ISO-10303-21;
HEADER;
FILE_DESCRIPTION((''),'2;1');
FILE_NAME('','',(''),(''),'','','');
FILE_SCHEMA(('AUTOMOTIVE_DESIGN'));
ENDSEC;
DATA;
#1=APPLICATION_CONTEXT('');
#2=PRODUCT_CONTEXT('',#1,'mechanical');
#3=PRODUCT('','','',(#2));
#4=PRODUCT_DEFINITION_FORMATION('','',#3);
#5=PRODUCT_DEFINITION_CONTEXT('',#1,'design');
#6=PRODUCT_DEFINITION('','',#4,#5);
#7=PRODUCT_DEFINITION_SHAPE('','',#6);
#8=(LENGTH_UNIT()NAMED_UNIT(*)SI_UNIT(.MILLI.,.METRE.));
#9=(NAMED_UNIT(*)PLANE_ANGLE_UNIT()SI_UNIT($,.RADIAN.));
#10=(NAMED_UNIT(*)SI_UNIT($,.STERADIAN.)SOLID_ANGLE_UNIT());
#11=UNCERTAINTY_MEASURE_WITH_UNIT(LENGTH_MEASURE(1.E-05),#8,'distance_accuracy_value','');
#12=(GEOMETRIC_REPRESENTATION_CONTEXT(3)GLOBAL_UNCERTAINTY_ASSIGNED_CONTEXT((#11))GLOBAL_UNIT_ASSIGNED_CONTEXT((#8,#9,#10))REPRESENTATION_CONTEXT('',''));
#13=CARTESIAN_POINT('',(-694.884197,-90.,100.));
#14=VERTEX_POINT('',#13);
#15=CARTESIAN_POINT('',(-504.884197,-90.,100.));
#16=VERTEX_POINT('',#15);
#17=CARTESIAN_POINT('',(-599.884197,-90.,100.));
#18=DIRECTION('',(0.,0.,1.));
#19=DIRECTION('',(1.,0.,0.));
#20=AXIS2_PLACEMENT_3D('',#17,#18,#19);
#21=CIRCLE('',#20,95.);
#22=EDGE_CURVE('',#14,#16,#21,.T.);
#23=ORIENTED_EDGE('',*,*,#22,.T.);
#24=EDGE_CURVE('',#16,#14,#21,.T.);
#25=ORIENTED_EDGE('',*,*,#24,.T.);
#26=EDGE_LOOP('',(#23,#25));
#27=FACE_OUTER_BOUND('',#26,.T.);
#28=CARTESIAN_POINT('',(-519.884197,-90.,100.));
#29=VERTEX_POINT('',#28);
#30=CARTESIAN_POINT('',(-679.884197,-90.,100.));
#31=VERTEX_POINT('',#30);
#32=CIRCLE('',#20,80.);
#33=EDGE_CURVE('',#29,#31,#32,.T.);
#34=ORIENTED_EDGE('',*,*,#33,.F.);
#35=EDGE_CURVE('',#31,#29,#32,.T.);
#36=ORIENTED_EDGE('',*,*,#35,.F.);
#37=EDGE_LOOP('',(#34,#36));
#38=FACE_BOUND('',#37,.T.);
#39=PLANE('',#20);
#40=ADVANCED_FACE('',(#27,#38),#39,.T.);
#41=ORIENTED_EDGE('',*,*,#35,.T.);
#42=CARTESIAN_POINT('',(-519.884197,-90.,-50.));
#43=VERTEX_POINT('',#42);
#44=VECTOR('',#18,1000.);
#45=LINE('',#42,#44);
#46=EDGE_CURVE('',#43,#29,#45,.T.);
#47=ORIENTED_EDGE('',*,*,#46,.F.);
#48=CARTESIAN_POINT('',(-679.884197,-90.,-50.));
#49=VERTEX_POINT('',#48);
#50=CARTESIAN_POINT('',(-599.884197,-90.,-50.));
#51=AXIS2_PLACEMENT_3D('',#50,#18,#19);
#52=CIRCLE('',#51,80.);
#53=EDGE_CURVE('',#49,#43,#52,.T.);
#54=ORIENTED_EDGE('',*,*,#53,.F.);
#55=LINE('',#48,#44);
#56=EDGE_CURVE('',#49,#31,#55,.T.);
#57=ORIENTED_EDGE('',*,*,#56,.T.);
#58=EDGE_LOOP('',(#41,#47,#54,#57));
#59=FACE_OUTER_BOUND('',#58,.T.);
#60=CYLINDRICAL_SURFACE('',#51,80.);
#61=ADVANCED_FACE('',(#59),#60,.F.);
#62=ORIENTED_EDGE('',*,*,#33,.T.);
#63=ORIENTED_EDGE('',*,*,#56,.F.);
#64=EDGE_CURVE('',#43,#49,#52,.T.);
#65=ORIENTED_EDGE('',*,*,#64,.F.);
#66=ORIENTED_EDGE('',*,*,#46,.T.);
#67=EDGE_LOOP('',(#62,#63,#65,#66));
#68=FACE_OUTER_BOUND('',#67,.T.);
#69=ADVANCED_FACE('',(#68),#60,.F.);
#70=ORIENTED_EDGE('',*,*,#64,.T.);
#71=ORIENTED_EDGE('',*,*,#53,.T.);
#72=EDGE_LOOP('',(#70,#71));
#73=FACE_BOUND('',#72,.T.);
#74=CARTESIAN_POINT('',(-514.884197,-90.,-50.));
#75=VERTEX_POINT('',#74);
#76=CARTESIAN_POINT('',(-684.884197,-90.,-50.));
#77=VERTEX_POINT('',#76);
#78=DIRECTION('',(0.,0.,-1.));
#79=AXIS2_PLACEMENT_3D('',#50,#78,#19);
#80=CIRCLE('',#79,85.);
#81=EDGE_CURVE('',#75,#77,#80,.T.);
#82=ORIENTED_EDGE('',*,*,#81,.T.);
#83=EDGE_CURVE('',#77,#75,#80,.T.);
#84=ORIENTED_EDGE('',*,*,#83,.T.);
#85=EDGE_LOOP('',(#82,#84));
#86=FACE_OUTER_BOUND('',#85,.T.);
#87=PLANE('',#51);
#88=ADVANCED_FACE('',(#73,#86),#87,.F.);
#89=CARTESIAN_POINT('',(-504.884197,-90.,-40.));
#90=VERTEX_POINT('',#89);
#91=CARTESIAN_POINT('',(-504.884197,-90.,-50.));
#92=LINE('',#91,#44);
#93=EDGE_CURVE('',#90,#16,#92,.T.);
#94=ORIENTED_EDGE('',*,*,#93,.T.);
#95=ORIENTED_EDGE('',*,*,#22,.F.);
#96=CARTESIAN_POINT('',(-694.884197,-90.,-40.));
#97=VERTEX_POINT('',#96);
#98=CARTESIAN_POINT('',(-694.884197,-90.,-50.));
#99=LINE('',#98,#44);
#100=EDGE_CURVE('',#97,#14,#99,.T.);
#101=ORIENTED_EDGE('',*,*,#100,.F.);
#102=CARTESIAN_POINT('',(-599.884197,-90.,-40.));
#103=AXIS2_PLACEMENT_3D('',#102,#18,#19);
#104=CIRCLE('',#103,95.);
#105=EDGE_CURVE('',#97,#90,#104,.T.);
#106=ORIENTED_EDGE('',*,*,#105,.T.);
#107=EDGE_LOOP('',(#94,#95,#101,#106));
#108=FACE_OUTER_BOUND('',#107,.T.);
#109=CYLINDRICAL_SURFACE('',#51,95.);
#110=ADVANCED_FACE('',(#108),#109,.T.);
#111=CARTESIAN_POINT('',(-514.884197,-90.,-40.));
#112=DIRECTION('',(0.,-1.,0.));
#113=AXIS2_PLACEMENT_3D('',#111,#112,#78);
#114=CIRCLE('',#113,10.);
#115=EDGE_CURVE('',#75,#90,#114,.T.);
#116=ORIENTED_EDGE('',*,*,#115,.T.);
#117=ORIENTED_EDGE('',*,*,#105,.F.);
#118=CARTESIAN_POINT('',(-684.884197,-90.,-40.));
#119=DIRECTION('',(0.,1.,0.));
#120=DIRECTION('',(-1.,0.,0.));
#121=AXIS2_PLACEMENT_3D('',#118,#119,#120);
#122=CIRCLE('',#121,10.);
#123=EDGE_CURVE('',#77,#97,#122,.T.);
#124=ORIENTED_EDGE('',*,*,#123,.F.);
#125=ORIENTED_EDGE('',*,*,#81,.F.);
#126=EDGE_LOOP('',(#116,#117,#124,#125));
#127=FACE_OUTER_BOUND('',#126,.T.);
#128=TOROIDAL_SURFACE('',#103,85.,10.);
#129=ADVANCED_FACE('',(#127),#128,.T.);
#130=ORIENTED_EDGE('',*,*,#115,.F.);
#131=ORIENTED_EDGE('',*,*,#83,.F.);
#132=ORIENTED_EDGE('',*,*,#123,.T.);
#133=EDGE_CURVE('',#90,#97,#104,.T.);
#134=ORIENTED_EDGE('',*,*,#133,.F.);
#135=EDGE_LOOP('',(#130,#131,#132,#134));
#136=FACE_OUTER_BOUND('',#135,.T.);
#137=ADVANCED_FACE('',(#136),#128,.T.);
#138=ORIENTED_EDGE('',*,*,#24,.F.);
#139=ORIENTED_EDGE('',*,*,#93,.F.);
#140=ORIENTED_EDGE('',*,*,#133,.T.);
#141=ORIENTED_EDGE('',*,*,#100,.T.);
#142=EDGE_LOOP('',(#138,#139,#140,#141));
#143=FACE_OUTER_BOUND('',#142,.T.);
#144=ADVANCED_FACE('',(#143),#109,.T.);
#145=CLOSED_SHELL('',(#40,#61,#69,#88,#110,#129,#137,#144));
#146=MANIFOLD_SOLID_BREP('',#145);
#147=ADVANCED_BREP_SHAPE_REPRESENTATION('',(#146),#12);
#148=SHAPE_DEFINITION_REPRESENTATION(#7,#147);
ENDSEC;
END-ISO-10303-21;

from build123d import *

# Parameters (mm, degrees)
BOSS_EXTRUDE1_DEPTH      = 100
BOSS_EXTRUDE1_DEPTH_BACK = 50
SKETCH1_R                = 95
SKETCH1_R_2              = 80
FILLET1_R                = 10


with BuildPart() as part:
    # Sketch1 → Boss-Extrude1 (new, two sides: drawn at the far end of the back side and taken through both)
    with BuildSketch(Plane.XY.offset(-BOSS_EXTRUDE1_DEPTH_BACK)):
        with Locations((-599.884196758, -90)):
            Circle(SKETCH1_R)
        with Locations((-599.884196758, -90)):
            Circle(SKETCH1_R_2, mode=Mode.SUBTRACT)
    extrude(amount=BOSS_EXTRUDE1_DEPTH + BOSS_EXTRUDE1_DEPTH_BACK)

    # Fillet1
    fillet1_edges = [part.edges().sort_by_distance(p)[0] for p in [
        (-694.884196758, -90, -50),
    ]]
    fillet(fillet1_edges, radius=FILLET1_R)


solid = part.part
